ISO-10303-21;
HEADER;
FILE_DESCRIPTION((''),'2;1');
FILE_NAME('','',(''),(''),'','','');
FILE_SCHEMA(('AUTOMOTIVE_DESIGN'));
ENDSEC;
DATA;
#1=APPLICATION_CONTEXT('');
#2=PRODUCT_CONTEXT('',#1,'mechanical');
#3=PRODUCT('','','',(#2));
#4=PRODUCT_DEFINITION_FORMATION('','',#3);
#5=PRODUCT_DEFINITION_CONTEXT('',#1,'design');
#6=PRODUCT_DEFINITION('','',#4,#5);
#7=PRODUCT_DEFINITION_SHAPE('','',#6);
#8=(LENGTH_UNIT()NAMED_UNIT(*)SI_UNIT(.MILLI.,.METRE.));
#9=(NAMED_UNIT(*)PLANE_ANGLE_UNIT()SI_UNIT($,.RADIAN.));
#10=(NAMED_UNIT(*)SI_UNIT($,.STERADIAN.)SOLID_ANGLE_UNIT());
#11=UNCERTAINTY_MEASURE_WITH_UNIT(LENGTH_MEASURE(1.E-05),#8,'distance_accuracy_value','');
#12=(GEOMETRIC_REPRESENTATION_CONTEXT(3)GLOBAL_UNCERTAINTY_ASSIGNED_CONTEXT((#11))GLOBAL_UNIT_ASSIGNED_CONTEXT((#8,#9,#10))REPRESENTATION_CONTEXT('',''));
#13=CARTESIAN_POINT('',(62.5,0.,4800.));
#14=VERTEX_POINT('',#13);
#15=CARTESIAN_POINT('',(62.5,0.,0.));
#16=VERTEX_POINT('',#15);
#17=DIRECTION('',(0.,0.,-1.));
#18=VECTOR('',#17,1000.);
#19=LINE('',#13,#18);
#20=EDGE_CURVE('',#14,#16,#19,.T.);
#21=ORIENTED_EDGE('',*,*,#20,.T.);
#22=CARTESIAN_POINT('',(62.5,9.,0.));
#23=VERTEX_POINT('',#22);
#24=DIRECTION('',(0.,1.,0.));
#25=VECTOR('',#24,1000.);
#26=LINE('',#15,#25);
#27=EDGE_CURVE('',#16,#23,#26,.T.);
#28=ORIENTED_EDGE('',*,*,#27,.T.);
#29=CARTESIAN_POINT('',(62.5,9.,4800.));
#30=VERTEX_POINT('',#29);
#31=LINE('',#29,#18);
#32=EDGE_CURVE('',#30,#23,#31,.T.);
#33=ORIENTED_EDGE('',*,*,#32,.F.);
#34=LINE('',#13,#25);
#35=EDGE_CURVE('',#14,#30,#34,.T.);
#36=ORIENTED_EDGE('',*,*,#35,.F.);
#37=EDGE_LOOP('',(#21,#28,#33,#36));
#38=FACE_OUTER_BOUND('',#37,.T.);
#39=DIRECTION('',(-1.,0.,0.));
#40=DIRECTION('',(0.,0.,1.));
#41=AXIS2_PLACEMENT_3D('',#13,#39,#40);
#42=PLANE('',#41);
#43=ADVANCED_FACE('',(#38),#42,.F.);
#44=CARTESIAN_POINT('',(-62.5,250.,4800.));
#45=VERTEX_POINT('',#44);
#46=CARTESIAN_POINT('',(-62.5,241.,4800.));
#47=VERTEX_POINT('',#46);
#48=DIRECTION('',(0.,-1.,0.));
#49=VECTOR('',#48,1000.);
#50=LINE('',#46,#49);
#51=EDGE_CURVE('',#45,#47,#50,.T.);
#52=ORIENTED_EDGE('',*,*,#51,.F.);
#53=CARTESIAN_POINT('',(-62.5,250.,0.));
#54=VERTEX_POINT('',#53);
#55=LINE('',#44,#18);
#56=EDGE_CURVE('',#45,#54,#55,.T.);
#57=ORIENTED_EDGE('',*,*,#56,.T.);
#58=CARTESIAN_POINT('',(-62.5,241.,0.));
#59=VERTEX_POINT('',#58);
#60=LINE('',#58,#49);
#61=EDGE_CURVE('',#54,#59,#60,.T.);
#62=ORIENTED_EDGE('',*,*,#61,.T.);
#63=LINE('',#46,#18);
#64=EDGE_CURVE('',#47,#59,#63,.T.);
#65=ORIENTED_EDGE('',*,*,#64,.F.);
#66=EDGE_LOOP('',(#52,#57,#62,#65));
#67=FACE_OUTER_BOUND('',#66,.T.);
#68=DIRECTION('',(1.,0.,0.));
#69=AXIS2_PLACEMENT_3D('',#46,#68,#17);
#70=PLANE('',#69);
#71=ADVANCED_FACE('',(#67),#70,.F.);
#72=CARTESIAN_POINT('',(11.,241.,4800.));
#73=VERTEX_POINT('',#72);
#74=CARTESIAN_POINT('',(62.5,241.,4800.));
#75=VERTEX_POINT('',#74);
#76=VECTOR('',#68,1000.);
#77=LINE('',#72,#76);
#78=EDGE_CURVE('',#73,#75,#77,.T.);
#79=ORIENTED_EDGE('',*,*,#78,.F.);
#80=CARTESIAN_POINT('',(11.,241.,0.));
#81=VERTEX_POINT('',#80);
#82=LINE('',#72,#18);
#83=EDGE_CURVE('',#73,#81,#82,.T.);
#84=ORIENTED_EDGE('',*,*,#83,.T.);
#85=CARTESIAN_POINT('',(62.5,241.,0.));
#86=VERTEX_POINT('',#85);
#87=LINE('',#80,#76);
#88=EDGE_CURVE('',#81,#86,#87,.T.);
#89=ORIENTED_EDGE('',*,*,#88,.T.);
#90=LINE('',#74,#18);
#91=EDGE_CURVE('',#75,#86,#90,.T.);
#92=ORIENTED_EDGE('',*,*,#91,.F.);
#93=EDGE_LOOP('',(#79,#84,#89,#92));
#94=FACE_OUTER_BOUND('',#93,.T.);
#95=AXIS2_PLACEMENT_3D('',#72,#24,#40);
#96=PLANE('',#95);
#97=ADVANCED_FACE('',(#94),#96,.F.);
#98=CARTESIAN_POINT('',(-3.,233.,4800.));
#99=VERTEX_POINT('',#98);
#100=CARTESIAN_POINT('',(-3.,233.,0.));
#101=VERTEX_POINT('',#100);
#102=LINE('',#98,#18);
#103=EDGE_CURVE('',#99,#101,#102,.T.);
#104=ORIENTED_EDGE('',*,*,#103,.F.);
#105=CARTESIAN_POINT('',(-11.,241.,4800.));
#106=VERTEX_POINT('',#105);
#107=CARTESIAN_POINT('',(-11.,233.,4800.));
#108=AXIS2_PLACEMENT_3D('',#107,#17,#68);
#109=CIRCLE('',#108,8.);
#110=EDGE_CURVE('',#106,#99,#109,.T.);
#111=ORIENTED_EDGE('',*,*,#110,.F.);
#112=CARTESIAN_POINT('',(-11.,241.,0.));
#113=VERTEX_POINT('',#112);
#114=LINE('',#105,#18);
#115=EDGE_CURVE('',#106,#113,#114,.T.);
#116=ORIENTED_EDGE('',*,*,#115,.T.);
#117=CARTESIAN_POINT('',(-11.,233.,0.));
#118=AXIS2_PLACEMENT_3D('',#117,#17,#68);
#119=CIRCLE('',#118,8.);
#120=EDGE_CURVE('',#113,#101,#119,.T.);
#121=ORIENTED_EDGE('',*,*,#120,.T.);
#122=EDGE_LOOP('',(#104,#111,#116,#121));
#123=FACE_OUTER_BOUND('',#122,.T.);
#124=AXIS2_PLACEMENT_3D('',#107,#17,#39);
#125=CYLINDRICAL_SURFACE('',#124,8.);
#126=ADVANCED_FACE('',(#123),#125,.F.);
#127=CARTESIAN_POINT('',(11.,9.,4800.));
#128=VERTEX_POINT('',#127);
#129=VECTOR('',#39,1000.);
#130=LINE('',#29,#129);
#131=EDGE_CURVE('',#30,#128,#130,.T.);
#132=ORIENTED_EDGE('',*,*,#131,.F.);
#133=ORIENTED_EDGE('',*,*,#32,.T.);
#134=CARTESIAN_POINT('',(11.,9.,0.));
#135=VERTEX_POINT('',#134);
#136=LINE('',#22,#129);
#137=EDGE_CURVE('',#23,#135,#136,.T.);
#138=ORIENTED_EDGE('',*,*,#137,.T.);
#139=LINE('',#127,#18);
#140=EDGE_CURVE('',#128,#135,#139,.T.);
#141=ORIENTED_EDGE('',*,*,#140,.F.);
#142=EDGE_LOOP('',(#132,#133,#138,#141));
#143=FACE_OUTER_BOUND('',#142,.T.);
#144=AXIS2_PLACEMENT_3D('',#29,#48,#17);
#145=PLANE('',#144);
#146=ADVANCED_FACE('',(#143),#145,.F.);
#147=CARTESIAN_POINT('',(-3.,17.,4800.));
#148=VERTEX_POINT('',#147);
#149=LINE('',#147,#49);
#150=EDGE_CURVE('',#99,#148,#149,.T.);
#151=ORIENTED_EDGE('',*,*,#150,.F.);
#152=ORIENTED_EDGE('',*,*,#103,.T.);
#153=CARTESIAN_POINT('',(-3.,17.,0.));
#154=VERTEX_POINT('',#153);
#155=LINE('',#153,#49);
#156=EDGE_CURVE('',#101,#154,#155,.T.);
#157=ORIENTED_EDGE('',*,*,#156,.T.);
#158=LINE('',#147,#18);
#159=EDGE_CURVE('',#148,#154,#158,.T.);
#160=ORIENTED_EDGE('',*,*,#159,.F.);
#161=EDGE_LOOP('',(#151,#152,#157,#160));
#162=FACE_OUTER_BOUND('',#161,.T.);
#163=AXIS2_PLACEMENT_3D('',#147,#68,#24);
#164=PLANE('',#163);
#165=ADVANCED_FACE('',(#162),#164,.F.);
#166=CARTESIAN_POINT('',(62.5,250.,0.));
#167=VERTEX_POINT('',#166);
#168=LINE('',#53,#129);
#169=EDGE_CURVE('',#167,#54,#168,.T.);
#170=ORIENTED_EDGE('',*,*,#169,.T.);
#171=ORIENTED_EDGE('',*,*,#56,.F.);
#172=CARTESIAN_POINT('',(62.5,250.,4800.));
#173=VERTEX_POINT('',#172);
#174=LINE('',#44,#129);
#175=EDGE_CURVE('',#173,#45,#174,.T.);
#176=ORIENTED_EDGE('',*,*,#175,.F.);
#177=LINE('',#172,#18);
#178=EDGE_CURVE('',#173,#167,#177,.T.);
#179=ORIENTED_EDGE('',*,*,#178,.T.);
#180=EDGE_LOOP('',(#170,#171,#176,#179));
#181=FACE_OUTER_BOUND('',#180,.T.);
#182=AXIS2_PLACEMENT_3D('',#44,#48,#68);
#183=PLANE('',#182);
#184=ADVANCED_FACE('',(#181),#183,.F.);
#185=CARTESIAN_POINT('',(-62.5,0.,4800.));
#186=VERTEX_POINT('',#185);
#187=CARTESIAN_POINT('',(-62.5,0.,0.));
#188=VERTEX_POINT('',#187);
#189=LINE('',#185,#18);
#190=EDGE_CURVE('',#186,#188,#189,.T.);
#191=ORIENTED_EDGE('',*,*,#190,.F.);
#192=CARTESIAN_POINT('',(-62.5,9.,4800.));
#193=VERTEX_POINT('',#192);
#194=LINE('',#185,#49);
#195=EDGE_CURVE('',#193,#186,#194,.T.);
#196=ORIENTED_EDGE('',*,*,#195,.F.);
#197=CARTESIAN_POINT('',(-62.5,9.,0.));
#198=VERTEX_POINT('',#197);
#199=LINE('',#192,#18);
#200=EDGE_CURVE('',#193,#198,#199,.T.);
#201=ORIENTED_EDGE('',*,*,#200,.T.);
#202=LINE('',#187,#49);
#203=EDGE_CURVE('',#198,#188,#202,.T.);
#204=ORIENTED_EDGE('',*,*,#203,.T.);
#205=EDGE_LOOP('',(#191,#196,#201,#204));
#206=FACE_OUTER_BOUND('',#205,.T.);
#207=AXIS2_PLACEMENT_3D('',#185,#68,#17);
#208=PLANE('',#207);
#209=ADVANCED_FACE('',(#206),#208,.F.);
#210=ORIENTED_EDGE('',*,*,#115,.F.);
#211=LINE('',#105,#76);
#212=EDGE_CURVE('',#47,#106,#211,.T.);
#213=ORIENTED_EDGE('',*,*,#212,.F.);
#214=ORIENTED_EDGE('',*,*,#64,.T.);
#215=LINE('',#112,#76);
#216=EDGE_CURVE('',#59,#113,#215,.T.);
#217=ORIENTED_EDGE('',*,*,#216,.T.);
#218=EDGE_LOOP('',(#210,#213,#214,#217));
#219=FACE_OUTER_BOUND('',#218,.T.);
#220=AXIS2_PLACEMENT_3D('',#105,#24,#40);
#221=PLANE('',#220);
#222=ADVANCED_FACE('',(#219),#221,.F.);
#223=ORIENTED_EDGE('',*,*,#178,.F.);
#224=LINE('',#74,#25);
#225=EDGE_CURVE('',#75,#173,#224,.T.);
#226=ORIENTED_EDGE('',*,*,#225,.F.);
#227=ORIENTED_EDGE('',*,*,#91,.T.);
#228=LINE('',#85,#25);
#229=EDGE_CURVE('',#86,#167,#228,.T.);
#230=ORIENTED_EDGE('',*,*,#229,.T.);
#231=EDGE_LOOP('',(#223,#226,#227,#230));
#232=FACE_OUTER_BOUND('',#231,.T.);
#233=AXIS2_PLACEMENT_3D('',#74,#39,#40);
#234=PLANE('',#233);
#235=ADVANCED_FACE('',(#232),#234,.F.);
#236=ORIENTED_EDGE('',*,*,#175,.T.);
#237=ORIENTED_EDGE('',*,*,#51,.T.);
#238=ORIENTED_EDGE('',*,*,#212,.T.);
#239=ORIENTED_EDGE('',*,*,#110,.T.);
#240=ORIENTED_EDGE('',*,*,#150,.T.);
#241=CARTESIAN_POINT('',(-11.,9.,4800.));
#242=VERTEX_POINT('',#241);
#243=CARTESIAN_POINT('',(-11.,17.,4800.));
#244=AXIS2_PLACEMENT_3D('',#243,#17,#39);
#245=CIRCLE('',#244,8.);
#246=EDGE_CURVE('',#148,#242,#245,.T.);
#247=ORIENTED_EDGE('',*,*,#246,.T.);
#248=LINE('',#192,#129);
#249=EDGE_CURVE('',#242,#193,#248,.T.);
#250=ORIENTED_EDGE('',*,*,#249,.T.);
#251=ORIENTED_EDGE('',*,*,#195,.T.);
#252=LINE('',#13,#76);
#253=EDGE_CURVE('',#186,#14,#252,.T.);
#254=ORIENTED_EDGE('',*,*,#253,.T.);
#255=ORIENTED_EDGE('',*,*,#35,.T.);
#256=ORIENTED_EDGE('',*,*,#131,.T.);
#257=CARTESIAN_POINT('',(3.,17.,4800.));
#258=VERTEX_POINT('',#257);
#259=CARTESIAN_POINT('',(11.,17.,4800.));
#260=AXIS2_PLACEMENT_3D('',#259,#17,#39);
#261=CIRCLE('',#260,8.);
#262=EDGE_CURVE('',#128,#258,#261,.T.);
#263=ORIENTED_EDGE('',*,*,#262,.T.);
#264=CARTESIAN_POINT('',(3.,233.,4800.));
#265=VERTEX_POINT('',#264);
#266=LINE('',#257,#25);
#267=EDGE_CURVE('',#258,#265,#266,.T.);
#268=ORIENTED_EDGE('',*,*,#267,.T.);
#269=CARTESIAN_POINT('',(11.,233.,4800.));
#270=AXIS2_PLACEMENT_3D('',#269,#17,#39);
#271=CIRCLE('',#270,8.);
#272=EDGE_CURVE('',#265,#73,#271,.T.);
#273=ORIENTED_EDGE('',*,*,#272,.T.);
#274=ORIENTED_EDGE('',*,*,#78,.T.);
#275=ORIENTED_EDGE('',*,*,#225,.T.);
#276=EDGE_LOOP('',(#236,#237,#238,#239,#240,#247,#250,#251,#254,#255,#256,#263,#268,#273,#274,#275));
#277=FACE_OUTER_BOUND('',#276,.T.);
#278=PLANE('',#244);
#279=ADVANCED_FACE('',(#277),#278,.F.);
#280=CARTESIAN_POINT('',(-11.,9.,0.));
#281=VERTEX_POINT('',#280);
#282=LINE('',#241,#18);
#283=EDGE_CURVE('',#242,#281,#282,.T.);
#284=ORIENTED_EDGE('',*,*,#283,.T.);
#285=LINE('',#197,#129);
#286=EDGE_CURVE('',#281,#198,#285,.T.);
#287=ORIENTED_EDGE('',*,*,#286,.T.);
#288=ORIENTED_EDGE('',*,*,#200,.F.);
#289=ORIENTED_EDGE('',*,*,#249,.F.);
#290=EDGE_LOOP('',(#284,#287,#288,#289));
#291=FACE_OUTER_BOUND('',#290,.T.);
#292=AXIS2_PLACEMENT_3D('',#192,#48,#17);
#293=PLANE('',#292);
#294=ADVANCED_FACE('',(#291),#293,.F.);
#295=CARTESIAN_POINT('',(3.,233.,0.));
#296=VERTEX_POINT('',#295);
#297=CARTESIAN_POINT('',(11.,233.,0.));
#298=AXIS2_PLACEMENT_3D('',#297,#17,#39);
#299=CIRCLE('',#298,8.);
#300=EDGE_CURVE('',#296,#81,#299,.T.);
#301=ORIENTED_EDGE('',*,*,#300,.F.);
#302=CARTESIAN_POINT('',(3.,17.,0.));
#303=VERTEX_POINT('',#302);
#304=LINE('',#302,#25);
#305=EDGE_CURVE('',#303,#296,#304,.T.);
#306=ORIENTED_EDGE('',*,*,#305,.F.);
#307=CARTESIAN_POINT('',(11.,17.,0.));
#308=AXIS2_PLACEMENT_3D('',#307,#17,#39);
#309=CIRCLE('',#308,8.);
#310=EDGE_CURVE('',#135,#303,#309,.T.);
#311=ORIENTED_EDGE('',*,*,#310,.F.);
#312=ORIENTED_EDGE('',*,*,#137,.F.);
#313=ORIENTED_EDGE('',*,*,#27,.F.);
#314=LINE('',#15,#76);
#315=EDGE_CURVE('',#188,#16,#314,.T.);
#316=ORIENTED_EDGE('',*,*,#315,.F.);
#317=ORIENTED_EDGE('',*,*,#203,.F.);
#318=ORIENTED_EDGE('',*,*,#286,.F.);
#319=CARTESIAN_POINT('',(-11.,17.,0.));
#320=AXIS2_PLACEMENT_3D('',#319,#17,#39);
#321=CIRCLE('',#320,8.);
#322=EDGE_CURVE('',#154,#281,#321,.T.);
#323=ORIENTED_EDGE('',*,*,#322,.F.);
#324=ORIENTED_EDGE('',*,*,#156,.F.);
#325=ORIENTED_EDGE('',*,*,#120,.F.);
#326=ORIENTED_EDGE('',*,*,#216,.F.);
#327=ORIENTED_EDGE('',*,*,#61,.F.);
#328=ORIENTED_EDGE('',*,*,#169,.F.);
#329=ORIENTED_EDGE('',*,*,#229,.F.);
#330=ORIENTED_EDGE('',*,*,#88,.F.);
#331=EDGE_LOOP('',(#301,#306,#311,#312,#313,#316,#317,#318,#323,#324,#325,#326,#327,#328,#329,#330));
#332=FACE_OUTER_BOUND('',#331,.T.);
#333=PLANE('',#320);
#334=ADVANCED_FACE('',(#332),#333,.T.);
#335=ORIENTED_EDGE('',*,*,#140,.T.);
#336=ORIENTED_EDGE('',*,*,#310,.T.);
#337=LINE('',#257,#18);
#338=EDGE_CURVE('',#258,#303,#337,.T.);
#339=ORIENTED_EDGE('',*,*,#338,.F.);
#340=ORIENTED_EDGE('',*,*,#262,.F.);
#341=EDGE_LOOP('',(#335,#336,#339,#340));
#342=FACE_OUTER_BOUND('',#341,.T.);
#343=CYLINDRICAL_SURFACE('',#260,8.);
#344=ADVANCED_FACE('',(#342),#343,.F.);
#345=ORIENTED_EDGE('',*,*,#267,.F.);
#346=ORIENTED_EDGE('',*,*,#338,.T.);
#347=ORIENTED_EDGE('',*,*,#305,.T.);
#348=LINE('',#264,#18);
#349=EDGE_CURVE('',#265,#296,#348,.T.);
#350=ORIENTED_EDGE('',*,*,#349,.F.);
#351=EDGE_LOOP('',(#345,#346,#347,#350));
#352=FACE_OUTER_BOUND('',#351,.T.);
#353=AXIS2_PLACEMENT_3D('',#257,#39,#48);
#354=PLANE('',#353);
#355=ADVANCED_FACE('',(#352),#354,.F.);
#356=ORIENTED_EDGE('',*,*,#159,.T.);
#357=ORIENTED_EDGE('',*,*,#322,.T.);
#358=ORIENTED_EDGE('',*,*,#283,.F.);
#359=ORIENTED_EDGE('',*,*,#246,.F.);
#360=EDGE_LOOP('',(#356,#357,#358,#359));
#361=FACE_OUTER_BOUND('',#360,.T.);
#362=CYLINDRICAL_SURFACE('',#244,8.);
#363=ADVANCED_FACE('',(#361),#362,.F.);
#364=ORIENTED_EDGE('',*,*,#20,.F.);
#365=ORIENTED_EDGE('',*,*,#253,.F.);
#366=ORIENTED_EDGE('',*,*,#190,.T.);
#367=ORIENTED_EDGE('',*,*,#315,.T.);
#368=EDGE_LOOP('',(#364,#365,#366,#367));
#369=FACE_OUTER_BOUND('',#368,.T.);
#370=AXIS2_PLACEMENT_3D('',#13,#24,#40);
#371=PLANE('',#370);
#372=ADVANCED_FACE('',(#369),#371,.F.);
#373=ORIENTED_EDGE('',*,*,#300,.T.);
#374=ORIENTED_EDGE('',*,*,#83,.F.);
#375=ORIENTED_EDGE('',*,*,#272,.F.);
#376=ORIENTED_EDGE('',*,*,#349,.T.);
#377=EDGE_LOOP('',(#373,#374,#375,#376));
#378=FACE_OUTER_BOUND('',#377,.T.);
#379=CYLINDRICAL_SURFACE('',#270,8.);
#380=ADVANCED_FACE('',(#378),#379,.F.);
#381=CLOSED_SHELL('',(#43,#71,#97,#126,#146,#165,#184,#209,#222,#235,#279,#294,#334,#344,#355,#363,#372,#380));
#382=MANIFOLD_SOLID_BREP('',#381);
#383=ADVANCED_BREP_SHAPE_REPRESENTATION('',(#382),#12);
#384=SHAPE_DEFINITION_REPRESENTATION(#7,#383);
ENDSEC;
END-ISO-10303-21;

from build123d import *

# Parameters (mm, degrees)
BOSS_EXTRUDE1_DEPTH = 4800


with BuildPart() as part:
    # Sketch1 → Boss-Extrude1 (new body)
    with BuildSketch(Plane.XY):
        with BuildLine():
            Line((62.5, 0), (-62.5, 0))
            Line((-62.5, 0), (-62.5, 9))
            Line((-62.5, 9), (-11, 9))
            ThreePointArc((-11, 9), (-5.343145751, 11.343145751), (-3, 17))
            Line((-3, 17), (-3, 233))
            ThreePointArc((-3, 233), (-5.343145751, 238.656854249), (-11, 241))
            Line((-11, 241), (-62.5, 241))
            Line((-62.5, 241), (-62.5, 250))
            Line((-62.5, 250), (62.5, 250))
            Line((62.5, 250), (62.5, 241))
            Line((62.5, 241), (11, 241))
            ThreePointArc((11, 241), (5.343145751, 238.656854249), (3, 233))
            Line((3, 233), (3, 17))
            ThreePointArc((3, 17), (5.343145751, 11.343145751), (11, 9))
            Line((11, 9), (62.5, 9))
            Line((62.5, 9), (62.5, 0))
        make_face()
    extrude(amount=BOSS_EXTRUDE1_DEPTH)


solid = part.part
